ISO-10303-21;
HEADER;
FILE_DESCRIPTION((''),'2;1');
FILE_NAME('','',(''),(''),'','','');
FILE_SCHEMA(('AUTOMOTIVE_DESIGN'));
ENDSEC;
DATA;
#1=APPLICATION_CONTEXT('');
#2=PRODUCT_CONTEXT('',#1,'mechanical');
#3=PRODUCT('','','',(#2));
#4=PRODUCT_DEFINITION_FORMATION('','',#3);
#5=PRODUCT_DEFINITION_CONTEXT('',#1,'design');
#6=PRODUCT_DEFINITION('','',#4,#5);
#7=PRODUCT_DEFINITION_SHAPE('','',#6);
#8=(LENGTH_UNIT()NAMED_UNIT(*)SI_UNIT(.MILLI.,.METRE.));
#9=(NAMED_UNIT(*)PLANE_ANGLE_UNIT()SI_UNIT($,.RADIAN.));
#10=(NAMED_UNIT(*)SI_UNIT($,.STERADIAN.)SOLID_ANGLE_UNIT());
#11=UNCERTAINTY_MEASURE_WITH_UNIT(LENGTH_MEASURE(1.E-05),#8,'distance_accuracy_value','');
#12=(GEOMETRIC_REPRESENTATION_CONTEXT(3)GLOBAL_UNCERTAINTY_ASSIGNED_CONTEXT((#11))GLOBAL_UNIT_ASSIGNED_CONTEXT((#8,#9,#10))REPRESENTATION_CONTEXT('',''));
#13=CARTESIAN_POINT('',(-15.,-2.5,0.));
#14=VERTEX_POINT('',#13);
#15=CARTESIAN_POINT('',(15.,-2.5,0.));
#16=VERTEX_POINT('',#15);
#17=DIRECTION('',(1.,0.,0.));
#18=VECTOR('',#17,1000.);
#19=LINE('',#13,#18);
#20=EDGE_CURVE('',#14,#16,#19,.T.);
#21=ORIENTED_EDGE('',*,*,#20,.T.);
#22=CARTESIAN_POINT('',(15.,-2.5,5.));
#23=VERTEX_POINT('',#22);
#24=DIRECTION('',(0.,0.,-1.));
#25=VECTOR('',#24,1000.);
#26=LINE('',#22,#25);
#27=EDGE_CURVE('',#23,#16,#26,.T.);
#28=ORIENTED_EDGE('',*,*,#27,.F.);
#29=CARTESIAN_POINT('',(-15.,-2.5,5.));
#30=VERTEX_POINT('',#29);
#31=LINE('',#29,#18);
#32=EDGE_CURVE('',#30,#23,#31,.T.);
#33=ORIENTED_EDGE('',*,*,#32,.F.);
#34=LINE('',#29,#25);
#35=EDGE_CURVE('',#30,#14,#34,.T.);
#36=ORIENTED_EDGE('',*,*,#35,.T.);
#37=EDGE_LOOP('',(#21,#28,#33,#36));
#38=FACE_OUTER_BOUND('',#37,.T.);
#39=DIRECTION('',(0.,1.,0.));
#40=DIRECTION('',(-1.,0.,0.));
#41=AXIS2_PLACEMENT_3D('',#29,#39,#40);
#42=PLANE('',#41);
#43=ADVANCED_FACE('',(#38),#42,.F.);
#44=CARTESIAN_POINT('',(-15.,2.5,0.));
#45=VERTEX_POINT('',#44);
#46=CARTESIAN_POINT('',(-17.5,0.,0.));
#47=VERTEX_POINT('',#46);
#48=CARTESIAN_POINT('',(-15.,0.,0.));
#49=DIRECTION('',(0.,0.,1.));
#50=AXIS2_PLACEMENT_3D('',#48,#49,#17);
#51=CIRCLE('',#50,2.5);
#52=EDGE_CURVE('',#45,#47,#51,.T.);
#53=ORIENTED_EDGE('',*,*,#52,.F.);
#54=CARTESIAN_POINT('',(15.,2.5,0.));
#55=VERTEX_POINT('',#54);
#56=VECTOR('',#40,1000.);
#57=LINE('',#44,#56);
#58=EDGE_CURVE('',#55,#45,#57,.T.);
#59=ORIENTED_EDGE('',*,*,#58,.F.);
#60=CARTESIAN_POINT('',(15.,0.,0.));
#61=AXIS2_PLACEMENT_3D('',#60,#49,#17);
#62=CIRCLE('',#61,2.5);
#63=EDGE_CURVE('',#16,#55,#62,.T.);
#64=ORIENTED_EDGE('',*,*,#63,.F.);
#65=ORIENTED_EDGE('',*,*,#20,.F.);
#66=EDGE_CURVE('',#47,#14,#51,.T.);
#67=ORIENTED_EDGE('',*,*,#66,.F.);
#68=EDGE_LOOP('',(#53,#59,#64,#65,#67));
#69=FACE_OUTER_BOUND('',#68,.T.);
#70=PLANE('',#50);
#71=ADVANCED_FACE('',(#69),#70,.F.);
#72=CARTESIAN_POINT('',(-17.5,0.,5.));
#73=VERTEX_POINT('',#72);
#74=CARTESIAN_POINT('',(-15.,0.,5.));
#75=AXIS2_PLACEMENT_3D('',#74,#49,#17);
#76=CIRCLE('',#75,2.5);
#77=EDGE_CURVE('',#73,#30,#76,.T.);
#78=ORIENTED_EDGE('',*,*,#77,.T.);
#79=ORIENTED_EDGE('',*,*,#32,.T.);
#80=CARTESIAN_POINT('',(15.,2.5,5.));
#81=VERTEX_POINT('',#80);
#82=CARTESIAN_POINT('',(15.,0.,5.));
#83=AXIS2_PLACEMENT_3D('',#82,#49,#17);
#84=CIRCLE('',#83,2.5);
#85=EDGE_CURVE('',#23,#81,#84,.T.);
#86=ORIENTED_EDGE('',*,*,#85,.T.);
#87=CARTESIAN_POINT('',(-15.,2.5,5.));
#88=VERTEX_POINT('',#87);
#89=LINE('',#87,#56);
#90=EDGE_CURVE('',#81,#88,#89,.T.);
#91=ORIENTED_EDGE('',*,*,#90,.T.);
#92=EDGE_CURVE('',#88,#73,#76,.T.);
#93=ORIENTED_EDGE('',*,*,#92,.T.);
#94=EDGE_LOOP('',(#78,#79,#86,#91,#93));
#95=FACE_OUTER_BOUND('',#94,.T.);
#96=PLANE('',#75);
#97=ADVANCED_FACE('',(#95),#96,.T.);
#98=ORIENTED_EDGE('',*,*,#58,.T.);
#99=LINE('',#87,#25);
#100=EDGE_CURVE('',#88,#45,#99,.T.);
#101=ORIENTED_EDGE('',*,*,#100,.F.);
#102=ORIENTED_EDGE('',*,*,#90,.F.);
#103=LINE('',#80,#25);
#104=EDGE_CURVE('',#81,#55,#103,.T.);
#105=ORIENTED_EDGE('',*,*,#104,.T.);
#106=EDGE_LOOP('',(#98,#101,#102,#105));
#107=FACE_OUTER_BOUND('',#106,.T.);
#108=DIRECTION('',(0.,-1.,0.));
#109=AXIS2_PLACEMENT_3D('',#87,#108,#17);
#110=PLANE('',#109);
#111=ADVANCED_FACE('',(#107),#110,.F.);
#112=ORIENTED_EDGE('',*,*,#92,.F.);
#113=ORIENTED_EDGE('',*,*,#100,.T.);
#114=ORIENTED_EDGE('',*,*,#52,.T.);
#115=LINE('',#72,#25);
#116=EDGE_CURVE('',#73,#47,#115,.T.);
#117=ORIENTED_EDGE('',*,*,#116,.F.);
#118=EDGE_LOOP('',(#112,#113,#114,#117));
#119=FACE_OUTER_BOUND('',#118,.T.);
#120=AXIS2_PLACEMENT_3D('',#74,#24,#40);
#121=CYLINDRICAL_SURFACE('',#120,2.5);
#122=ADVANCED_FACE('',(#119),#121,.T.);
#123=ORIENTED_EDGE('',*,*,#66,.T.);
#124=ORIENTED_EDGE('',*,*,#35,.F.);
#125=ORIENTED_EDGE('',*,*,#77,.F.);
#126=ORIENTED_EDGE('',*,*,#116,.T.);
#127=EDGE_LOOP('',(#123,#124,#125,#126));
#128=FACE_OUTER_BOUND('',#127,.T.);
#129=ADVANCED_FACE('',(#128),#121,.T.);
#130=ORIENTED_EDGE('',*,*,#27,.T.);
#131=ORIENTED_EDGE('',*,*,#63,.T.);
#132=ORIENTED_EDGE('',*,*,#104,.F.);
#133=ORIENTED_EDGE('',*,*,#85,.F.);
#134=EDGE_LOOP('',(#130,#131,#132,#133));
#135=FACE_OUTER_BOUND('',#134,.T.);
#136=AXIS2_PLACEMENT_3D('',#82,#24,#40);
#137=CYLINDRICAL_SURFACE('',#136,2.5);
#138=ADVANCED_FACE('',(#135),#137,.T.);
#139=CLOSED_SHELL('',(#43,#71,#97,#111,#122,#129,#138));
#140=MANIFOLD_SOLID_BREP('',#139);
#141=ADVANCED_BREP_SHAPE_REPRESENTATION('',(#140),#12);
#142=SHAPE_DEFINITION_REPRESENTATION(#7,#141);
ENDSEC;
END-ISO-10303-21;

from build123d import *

# Parameters (mm, degrees)
BOSS_EXTRUDE1_DEPTH = 5


with BuildPart() as part:
    # Sketch1 → Boss-Extrude1 (new body)
    with BuildSketch(Plane.XY):
        with BuildLine():
            Line((-15, 2.5), (15, 2.5))
            ThreePointArc((15, 2.5), (17.5, 0), (15, -2.5))
            Line((15, -2.5), (-15, -2.5))
            ThreePointArc((-15, -2.5), (-17.5, 0), (-15, 2.5))
        make_face()
    extrude(amount=BOSS_EXTRUDE1_DEPTH)


solid = part.part
